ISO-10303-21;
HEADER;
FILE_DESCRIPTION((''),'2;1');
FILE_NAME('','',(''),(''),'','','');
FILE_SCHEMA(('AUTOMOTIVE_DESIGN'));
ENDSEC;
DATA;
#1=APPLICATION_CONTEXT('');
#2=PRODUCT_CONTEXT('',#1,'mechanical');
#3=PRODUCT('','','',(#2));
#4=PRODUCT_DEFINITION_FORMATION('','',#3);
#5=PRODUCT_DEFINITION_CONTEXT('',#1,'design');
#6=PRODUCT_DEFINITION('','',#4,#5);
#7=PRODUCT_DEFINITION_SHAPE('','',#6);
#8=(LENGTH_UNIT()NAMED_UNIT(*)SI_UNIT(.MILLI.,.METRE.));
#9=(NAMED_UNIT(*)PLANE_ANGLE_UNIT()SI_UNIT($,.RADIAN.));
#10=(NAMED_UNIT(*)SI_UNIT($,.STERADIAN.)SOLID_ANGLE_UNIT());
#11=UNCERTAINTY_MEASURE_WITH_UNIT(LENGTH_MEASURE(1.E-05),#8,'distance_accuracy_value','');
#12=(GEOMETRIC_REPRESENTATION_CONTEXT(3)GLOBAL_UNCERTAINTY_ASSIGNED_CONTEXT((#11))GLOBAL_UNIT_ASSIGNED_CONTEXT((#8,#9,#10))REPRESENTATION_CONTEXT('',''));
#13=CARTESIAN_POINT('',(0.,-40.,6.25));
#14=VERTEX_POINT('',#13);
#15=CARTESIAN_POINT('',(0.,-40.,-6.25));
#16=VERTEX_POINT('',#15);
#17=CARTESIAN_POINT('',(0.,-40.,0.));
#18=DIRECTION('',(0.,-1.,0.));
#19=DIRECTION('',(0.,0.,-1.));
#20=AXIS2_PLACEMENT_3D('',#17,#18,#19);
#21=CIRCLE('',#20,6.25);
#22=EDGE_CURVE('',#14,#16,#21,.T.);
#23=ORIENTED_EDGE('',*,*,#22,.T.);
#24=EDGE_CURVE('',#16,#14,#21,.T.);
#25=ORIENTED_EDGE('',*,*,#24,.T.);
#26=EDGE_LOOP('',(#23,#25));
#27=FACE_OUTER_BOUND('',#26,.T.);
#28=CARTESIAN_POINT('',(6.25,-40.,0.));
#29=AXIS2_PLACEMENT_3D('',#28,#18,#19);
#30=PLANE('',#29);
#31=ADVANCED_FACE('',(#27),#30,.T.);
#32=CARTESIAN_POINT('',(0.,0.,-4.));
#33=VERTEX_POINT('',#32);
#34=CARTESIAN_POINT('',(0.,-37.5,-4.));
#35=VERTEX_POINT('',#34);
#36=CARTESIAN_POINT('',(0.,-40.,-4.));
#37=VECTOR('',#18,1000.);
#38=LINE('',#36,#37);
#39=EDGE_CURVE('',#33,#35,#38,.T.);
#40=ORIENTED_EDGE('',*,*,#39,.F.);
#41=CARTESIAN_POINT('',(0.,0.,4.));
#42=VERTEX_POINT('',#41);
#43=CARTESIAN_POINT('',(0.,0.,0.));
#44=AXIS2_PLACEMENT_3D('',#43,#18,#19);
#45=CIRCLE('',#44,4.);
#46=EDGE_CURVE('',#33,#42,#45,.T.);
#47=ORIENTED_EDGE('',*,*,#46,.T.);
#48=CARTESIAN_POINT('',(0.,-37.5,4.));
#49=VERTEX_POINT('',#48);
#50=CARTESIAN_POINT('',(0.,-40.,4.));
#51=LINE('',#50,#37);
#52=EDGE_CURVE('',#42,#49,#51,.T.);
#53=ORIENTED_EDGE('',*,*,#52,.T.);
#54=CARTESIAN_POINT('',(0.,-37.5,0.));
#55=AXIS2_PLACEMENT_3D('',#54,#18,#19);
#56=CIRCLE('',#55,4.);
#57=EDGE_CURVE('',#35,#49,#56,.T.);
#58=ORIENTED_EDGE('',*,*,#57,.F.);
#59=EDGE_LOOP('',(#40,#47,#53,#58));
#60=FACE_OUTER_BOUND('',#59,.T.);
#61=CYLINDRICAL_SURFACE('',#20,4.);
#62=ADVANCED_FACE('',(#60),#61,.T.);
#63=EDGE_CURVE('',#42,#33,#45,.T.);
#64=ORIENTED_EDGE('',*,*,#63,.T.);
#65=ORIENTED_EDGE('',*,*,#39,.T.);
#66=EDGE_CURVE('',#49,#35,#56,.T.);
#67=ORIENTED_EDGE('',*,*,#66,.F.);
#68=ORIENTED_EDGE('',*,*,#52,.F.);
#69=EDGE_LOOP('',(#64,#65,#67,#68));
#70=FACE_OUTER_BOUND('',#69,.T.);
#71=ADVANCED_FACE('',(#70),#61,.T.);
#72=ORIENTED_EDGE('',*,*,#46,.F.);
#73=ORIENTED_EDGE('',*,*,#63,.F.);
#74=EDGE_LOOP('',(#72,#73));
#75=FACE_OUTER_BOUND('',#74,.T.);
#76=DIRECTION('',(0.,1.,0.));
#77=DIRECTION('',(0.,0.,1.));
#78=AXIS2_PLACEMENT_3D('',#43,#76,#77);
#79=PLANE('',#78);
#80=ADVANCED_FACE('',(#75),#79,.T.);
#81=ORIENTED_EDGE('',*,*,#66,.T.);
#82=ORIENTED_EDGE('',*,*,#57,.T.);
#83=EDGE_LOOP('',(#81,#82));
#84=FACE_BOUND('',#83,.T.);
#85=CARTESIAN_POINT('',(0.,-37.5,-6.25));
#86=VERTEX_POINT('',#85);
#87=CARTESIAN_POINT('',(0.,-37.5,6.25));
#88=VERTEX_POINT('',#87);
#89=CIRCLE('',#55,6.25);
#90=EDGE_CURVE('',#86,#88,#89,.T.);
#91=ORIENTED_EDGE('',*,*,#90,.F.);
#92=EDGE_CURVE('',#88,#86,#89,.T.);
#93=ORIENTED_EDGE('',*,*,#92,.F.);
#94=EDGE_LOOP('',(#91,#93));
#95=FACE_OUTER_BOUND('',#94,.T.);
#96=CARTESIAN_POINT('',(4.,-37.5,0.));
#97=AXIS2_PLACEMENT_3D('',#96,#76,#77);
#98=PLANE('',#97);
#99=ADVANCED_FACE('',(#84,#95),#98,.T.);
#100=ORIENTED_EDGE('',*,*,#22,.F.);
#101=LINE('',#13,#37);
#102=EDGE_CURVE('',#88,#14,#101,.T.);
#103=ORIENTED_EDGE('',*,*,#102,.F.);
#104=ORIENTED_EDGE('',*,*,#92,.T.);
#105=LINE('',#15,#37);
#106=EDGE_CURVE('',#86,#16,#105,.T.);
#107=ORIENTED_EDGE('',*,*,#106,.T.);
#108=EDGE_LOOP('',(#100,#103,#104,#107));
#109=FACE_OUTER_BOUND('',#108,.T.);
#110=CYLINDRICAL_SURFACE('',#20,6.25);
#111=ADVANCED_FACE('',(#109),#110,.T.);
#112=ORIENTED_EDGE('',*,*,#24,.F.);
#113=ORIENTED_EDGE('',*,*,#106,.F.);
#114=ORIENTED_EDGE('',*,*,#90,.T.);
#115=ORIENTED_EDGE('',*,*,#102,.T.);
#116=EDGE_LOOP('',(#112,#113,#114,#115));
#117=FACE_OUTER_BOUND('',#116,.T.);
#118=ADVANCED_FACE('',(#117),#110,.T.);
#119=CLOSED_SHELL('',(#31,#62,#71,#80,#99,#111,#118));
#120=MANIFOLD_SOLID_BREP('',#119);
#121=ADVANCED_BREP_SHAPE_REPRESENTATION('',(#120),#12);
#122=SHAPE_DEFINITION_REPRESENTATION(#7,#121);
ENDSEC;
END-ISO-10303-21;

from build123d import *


with BuildPart() as part:
    # 草图1 → 旋转1 (revolve)
    with BuildSketch(Plane.XY, mode=Mode.PRIVATE) as revolve_1_sk:
        Polygon((0, 0), (4, 0), (4, -37.5), (6.25, -37.5), (6.25, -40), (0, -40), align=None)
    revolve(revolve_1_sk.sketch.rotate(Axis((0, -40, 0), (0, 1, 0)), 90), axis=Axis((0, -40, 0), (0, 1, 0)))


solid = part.part
